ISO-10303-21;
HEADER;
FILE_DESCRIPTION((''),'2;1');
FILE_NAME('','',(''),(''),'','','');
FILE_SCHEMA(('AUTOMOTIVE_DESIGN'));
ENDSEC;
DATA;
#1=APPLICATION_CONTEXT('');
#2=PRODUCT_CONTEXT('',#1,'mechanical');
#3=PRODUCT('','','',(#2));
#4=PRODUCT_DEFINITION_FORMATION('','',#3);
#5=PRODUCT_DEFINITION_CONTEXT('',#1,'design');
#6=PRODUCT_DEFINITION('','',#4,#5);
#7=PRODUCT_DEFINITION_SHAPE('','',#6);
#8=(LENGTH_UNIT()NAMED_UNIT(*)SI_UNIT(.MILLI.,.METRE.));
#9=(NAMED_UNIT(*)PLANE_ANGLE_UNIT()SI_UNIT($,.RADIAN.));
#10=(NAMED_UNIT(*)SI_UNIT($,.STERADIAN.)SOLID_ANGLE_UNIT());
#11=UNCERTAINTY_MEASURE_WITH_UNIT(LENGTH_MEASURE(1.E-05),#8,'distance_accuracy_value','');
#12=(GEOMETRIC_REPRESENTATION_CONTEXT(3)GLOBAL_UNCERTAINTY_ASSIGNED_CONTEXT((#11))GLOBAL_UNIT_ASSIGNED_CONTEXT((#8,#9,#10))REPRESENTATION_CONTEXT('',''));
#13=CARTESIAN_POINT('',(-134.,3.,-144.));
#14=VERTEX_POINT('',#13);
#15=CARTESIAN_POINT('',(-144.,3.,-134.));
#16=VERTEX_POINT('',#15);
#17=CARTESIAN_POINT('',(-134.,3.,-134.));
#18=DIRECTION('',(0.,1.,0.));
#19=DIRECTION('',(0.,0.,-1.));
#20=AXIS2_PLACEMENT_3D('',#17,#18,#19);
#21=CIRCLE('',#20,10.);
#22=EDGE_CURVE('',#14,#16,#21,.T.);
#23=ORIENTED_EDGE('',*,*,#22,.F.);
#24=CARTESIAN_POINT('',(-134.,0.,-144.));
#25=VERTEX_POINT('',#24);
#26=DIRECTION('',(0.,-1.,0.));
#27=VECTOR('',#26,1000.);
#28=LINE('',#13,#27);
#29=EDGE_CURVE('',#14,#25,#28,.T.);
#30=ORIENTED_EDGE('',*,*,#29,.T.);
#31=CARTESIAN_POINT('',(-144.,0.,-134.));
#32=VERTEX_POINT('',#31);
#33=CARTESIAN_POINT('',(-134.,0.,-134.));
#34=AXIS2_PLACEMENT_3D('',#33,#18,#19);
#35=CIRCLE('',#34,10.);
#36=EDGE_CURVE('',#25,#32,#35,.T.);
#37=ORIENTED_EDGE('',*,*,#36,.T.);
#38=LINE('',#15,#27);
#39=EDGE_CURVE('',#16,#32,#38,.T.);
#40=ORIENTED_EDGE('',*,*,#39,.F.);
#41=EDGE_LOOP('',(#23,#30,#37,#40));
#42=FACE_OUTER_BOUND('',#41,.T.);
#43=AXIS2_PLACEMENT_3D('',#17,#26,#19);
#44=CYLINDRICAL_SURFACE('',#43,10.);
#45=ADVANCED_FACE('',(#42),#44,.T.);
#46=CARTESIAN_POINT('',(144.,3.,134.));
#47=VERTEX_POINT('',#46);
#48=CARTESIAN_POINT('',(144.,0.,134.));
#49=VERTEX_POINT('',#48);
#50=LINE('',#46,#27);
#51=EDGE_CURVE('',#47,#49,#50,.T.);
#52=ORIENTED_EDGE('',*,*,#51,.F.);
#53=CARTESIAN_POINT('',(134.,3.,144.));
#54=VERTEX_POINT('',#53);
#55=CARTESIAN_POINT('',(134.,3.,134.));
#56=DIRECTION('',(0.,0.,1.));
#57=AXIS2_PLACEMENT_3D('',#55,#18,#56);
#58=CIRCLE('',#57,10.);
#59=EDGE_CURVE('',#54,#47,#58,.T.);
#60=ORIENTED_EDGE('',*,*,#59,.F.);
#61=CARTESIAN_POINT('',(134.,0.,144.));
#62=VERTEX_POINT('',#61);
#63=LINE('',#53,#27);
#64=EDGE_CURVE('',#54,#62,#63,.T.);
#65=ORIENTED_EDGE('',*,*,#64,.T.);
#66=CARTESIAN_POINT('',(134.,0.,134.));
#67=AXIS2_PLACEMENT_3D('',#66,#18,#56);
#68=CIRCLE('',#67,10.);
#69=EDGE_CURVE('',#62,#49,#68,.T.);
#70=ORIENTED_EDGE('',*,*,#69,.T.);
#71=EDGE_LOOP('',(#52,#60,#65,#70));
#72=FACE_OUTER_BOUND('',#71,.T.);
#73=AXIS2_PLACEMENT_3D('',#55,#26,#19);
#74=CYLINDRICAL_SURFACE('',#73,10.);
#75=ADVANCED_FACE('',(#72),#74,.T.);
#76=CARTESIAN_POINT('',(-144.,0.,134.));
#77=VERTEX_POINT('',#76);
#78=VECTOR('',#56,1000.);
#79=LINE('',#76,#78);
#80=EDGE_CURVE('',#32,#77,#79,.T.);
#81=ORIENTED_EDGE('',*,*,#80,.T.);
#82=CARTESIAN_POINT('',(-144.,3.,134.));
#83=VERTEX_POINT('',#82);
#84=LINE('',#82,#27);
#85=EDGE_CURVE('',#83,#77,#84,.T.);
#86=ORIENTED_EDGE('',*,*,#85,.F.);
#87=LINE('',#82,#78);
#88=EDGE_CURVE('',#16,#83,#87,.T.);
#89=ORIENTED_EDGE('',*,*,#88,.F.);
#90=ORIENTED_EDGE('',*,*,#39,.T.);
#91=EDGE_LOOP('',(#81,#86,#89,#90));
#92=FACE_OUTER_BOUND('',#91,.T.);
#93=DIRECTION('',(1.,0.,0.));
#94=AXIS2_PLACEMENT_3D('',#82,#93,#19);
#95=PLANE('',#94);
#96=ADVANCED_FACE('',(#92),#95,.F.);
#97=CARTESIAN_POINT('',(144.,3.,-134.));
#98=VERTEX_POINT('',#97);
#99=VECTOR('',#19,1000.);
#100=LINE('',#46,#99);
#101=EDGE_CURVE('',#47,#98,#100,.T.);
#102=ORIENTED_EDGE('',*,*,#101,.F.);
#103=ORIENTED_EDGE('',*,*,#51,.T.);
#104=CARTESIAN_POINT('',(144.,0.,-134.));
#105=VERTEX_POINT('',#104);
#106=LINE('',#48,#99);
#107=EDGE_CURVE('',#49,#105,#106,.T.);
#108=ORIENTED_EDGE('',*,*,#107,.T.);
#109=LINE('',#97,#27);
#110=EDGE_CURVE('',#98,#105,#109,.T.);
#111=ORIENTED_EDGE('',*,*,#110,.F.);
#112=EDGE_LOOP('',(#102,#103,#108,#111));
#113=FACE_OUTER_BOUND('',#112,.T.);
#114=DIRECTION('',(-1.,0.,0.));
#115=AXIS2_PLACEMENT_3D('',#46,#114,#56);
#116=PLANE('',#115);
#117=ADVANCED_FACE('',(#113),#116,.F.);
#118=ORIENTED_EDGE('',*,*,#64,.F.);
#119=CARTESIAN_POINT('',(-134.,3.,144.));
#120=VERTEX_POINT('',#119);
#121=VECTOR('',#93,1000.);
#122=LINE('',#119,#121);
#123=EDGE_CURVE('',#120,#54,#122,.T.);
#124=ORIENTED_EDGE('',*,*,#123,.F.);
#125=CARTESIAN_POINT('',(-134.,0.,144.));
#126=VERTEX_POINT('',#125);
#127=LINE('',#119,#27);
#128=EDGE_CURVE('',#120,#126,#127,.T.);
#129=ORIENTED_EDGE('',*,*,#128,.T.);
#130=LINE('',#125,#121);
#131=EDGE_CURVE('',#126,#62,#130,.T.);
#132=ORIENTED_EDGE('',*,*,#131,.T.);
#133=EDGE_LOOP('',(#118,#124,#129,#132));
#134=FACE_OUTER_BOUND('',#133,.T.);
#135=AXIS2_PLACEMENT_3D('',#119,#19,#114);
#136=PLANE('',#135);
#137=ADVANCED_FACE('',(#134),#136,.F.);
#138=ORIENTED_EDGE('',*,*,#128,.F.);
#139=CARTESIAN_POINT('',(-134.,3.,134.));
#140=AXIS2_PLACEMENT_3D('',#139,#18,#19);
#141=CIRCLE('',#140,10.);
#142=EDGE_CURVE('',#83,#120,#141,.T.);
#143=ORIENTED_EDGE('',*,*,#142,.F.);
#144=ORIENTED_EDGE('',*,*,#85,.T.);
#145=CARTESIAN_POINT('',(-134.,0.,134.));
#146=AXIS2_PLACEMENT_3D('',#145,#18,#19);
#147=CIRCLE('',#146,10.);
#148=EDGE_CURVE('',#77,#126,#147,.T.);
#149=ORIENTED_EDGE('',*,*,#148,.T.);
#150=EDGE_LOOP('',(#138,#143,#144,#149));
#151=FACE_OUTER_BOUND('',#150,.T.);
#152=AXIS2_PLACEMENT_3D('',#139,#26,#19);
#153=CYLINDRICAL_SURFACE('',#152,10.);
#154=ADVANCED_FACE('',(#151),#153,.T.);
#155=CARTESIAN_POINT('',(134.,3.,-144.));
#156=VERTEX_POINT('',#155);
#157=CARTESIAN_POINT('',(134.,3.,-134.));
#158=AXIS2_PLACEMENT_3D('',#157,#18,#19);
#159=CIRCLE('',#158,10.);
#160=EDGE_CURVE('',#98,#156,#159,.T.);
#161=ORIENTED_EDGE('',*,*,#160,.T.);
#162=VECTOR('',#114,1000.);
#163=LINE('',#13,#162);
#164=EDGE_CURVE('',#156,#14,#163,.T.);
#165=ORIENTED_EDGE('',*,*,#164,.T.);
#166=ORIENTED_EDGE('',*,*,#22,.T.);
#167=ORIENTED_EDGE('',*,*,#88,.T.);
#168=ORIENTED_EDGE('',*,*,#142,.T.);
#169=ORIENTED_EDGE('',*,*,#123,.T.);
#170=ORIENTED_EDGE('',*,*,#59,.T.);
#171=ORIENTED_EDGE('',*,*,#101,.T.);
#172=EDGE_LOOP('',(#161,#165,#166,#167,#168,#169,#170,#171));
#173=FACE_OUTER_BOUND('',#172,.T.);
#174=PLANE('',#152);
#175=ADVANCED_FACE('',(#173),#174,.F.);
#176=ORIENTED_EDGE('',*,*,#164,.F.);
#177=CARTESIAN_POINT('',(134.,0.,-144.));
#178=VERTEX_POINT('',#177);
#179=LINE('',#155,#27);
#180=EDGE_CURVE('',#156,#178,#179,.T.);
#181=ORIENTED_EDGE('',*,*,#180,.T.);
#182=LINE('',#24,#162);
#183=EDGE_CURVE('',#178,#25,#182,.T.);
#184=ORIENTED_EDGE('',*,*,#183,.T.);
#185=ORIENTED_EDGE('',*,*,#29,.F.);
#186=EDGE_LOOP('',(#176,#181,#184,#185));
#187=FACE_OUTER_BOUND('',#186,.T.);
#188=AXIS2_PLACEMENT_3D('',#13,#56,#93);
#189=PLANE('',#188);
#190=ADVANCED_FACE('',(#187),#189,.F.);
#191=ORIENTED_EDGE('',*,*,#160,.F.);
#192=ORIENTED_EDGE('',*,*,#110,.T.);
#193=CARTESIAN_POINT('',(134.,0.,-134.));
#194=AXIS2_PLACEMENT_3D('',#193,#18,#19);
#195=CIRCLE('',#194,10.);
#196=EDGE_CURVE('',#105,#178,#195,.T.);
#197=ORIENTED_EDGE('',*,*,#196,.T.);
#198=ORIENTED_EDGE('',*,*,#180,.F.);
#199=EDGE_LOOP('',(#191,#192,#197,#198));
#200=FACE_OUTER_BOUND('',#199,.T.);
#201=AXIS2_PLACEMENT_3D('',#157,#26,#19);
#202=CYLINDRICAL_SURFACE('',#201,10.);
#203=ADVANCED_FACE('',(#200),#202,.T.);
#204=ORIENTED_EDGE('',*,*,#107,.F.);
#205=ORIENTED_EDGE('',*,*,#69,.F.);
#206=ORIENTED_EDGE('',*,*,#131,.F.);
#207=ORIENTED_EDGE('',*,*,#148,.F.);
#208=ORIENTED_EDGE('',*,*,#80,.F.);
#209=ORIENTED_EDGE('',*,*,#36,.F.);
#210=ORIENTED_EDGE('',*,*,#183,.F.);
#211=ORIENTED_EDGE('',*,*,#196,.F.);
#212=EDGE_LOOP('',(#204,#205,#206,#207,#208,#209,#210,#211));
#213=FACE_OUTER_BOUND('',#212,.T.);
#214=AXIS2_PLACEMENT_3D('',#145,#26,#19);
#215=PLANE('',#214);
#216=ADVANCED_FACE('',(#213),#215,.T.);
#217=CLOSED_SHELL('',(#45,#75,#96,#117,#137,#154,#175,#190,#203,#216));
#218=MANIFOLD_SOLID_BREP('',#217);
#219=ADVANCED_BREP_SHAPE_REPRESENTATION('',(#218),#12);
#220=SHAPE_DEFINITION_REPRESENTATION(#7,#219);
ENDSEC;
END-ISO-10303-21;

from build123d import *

# Parameters (mm, degrees)
BOSS_EXTRUDE1_DEPTH = 3


with BuildPart() as part:
    # Sketch1 → Boss-Extrude1 (new body)
    with BuildSketch(Plane(origin=(0, 0, 0), x_dir=(1, 0, 0), z_dir=(0, 1, 0))):
        with BuildLine():
            Line((-134, -144), (134, -144))
            ThreePointArc((134, -144), (141.071067812, -141.071067812), (144, -134))
            Line((144, -134), (144, 134))
            ThreePointArc((144, 134), (141.071067812, 141.071067812), (134, 144))
            Line((134, 144), (-134, 144))
            ThreePointArc((-134, 144), (-141.071067812, 141.071067812), (-144, 134))
            Line((-144, 134), (-144, -134))
            ThreePointArc((-144, -134), (-141.071067812, -141.071067812), (-134, -144))
        make_face()
    extrude(amount=BOSS_EXTRUDE1_DEPTH)


solid = part.part
